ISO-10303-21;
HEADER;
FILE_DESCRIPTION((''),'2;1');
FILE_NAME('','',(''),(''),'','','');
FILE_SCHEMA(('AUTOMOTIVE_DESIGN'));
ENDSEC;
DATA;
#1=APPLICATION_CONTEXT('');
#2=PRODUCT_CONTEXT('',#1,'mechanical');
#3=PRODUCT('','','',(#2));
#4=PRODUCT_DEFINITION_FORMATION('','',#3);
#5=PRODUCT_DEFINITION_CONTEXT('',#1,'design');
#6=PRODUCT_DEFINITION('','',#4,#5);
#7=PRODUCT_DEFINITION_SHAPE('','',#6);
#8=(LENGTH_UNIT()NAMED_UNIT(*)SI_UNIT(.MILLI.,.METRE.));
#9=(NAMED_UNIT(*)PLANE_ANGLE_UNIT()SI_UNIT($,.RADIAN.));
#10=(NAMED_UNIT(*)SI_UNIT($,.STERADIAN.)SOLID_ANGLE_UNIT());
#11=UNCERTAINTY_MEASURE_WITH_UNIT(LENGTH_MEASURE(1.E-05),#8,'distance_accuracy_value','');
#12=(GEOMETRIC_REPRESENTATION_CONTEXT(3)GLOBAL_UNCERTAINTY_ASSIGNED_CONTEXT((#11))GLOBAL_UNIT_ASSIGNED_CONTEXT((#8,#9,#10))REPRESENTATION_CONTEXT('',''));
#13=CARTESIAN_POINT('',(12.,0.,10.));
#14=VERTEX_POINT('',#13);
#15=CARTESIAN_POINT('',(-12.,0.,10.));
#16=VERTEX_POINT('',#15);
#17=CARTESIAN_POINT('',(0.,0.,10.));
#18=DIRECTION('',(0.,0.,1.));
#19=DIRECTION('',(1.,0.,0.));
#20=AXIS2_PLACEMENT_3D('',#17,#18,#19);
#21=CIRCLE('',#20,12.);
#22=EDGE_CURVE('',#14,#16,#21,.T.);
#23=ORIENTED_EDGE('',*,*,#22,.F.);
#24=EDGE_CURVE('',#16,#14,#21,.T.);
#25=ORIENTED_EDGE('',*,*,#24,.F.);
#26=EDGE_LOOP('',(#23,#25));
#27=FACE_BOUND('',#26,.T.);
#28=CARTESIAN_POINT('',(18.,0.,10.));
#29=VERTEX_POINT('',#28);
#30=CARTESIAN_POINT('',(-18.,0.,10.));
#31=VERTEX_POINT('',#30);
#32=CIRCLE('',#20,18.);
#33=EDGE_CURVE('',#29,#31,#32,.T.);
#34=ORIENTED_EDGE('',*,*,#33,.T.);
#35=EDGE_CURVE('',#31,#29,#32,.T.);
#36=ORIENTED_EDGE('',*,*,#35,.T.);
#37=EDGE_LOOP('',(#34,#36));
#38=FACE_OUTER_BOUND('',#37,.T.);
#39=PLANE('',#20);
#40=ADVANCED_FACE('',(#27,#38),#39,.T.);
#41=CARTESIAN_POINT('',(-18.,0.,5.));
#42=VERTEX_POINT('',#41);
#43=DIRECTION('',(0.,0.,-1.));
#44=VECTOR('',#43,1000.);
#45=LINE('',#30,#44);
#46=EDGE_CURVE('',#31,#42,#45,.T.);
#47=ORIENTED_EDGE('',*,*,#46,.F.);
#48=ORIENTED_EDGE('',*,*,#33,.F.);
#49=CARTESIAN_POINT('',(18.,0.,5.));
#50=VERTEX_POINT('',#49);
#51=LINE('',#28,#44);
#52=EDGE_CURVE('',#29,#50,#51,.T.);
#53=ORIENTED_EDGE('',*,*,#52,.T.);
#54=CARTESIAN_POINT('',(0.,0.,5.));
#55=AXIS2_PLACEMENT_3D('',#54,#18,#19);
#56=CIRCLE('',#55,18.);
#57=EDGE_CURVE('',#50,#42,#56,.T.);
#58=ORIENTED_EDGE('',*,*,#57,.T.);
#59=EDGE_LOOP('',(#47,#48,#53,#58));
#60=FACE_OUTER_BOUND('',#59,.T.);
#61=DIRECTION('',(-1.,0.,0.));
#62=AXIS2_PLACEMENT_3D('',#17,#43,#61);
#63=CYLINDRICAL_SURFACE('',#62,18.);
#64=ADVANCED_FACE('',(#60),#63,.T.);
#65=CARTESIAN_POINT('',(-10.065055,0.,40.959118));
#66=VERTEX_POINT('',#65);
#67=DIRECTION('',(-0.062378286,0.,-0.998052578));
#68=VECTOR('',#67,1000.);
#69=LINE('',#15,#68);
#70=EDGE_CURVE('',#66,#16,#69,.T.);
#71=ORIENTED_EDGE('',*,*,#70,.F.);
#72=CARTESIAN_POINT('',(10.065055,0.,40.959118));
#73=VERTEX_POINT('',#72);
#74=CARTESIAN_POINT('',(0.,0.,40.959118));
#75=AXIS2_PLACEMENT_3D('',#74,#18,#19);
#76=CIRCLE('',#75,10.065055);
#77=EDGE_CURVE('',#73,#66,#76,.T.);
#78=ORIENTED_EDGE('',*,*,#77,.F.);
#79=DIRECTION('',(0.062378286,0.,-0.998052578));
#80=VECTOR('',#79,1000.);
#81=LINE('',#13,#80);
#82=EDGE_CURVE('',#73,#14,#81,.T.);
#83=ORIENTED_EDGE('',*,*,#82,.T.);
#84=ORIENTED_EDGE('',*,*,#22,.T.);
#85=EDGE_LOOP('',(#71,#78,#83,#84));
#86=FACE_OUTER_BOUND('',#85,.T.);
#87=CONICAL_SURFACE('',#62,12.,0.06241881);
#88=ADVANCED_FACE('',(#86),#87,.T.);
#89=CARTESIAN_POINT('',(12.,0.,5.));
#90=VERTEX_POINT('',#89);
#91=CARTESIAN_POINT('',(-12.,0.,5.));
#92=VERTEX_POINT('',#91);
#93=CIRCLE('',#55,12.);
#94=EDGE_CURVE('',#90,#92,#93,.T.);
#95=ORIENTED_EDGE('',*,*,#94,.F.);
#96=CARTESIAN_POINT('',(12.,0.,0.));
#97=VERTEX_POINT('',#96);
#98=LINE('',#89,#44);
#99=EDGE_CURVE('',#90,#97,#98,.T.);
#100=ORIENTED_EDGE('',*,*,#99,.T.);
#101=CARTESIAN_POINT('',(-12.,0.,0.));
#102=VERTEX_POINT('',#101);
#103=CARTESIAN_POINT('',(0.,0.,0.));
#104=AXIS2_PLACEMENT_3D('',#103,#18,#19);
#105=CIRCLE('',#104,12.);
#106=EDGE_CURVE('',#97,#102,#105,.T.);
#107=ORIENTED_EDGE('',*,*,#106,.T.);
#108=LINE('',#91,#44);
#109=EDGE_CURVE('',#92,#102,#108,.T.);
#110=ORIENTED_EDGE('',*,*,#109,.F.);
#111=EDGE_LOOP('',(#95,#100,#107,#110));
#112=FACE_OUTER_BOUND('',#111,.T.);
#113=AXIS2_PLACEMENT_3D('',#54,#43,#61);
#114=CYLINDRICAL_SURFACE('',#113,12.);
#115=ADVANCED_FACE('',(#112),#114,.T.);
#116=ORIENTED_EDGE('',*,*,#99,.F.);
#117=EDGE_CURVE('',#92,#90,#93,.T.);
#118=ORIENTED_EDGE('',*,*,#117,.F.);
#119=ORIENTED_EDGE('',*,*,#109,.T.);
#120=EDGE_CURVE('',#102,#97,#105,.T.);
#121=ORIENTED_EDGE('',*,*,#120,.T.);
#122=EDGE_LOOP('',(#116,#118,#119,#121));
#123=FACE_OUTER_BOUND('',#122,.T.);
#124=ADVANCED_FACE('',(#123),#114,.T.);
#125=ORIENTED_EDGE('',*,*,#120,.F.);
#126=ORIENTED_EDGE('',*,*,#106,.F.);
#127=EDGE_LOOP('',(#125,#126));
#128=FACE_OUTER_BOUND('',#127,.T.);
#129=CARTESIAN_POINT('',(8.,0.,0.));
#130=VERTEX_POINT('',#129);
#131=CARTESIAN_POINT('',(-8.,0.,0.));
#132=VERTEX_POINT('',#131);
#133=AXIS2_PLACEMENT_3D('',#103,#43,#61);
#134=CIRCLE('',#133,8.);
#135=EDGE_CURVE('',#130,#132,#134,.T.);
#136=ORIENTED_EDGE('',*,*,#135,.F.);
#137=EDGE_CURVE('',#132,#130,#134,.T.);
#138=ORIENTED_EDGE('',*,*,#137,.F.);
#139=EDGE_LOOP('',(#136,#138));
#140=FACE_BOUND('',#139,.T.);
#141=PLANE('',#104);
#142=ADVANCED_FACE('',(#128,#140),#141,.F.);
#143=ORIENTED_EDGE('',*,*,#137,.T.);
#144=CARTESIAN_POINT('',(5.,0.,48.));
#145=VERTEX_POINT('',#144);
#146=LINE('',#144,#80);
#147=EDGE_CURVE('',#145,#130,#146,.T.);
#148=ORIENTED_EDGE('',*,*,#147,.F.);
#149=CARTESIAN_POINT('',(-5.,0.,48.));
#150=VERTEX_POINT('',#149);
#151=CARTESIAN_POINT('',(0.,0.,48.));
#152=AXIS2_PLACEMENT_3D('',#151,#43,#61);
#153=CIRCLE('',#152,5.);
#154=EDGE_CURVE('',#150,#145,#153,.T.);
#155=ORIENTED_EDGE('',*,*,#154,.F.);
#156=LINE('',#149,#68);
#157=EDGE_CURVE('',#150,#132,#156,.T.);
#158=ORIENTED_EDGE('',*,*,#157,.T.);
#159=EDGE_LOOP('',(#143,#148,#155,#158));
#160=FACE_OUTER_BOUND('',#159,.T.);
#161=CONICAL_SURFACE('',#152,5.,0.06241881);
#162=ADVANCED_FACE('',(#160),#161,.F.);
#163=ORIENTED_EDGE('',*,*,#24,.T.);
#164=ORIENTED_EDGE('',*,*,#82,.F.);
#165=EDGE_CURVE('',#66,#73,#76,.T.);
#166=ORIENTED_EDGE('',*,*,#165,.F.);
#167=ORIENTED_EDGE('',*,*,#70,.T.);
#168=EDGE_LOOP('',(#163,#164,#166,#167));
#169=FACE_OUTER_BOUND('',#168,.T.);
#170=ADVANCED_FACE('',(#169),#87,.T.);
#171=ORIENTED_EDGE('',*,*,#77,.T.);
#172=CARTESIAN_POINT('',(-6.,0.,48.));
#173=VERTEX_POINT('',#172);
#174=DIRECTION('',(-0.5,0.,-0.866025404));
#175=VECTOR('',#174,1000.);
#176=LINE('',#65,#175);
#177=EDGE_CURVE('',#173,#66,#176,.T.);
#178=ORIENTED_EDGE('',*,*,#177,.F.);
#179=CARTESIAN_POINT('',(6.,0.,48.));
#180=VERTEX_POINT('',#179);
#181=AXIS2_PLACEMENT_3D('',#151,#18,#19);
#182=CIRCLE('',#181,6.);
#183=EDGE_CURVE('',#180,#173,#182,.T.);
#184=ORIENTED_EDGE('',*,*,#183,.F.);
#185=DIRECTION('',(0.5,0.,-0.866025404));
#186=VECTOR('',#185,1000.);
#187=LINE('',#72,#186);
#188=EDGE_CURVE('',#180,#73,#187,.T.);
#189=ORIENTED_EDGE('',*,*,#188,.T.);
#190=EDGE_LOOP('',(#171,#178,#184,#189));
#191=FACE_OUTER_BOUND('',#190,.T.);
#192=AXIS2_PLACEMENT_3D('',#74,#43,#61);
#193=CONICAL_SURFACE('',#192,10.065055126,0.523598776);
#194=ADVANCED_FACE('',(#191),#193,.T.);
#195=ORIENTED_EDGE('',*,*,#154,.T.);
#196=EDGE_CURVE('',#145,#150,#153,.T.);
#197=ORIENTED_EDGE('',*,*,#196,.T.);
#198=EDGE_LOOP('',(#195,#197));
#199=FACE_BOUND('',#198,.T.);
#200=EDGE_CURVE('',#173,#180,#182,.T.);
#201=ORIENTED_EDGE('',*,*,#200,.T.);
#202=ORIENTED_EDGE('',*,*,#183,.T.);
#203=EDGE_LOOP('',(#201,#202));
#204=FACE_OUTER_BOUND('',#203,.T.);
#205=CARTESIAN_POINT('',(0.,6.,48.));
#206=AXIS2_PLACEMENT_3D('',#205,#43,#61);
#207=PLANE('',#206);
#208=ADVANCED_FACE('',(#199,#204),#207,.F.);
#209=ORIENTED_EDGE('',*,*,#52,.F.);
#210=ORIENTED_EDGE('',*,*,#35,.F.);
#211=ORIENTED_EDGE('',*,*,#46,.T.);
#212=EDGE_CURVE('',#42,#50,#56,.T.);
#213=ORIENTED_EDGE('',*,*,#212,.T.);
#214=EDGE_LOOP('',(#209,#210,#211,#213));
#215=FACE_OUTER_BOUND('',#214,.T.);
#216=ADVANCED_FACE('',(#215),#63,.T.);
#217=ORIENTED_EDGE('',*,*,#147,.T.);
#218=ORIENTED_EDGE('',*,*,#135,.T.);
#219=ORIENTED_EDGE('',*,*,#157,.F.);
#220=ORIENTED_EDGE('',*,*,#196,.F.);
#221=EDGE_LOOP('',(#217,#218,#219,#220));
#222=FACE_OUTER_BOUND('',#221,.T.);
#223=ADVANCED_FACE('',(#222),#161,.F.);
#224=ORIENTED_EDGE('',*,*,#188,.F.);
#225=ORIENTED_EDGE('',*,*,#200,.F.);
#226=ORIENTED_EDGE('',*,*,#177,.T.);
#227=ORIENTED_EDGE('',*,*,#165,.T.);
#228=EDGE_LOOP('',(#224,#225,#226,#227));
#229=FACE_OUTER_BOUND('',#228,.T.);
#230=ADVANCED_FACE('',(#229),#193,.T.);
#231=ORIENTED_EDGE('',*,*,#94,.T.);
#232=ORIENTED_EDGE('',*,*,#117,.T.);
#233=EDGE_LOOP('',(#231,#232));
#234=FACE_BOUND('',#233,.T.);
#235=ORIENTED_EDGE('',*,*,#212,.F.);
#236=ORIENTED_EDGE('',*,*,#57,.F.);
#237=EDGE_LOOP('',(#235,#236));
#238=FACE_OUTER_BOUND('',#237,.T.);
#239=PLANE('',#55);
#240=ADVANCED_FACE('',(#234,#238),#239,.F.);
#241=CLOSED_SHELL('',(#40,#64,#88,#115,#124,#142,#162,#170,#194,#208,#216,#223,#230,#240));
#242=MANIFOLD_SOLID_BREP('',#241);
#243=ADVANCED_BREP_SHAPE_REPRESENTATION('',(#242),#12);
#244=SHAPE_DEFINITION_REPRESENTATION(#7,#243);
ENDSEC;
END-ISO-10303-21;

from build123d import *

# Parameters (mm, degrees)
SKETCH1_R           = 12
BOSS_EXTRUDE1_DEPTH = 5
SKETCH2_R           = 18
BOSS_EXTRUDE2_DEPTH = 5


with BuildPart() as part:
    # Sketch1 → Boss-Extrude1 (new body)
    with BuildSketch(Plane.XY):
        Circle(SKETCH1_R)
    extrude(amount=BOSS_EXTRUDE1_DEPTH)

    # Sketch2 → Boss-Extrude2 (add)
    with BuildSketch(Plane.XY.offset(5)):
        Circle(SKETCH2_R)
    extrude(amount=BOSS_EXTRUDE2_DEPTH)

    # Sketch3 → Revolve1 (revolve)
    with BuildSketch(Plane(origin=(0, 0, 0), x_dir=(0, 0, -1), z_dir=(1, 0, 0)), mode=Mode.PRIVATE) as revolve1_sk:
        Polygon((-10, 0), (-10, 12), (-40.959117986, 10.065055126), (-48, 6), (-48, 0), align=None)
    revolve(revolve1_sk.sketch.rotate(Axis((0, 0, 48), (0, 0, -1)), 90), axis=Axis((0, 0, 48), (0, 0, -1)))

    # Sketch5 → Cut-Revolve1 (revolve, cut)
    with BuildSketch(Plane(origin=(0, 0, 0), x_dir=(1, 0, 0), z_dir=(0, 1, 0)), mode=Mode.PRIVATE) as cut_revolve1_sk:
        Polygon((0, -48), (5, -48), (8, 0), (0, 0), align=None)
    revolve(cut_revolve1_sk.sketch.rotate(Axis((0, 0, 0), (0, 0, 1)), 180), axis=Axis((0, 0, 0), (0, 0, 1)), mode=Mode.SUBTRACT)


solid = part.part
